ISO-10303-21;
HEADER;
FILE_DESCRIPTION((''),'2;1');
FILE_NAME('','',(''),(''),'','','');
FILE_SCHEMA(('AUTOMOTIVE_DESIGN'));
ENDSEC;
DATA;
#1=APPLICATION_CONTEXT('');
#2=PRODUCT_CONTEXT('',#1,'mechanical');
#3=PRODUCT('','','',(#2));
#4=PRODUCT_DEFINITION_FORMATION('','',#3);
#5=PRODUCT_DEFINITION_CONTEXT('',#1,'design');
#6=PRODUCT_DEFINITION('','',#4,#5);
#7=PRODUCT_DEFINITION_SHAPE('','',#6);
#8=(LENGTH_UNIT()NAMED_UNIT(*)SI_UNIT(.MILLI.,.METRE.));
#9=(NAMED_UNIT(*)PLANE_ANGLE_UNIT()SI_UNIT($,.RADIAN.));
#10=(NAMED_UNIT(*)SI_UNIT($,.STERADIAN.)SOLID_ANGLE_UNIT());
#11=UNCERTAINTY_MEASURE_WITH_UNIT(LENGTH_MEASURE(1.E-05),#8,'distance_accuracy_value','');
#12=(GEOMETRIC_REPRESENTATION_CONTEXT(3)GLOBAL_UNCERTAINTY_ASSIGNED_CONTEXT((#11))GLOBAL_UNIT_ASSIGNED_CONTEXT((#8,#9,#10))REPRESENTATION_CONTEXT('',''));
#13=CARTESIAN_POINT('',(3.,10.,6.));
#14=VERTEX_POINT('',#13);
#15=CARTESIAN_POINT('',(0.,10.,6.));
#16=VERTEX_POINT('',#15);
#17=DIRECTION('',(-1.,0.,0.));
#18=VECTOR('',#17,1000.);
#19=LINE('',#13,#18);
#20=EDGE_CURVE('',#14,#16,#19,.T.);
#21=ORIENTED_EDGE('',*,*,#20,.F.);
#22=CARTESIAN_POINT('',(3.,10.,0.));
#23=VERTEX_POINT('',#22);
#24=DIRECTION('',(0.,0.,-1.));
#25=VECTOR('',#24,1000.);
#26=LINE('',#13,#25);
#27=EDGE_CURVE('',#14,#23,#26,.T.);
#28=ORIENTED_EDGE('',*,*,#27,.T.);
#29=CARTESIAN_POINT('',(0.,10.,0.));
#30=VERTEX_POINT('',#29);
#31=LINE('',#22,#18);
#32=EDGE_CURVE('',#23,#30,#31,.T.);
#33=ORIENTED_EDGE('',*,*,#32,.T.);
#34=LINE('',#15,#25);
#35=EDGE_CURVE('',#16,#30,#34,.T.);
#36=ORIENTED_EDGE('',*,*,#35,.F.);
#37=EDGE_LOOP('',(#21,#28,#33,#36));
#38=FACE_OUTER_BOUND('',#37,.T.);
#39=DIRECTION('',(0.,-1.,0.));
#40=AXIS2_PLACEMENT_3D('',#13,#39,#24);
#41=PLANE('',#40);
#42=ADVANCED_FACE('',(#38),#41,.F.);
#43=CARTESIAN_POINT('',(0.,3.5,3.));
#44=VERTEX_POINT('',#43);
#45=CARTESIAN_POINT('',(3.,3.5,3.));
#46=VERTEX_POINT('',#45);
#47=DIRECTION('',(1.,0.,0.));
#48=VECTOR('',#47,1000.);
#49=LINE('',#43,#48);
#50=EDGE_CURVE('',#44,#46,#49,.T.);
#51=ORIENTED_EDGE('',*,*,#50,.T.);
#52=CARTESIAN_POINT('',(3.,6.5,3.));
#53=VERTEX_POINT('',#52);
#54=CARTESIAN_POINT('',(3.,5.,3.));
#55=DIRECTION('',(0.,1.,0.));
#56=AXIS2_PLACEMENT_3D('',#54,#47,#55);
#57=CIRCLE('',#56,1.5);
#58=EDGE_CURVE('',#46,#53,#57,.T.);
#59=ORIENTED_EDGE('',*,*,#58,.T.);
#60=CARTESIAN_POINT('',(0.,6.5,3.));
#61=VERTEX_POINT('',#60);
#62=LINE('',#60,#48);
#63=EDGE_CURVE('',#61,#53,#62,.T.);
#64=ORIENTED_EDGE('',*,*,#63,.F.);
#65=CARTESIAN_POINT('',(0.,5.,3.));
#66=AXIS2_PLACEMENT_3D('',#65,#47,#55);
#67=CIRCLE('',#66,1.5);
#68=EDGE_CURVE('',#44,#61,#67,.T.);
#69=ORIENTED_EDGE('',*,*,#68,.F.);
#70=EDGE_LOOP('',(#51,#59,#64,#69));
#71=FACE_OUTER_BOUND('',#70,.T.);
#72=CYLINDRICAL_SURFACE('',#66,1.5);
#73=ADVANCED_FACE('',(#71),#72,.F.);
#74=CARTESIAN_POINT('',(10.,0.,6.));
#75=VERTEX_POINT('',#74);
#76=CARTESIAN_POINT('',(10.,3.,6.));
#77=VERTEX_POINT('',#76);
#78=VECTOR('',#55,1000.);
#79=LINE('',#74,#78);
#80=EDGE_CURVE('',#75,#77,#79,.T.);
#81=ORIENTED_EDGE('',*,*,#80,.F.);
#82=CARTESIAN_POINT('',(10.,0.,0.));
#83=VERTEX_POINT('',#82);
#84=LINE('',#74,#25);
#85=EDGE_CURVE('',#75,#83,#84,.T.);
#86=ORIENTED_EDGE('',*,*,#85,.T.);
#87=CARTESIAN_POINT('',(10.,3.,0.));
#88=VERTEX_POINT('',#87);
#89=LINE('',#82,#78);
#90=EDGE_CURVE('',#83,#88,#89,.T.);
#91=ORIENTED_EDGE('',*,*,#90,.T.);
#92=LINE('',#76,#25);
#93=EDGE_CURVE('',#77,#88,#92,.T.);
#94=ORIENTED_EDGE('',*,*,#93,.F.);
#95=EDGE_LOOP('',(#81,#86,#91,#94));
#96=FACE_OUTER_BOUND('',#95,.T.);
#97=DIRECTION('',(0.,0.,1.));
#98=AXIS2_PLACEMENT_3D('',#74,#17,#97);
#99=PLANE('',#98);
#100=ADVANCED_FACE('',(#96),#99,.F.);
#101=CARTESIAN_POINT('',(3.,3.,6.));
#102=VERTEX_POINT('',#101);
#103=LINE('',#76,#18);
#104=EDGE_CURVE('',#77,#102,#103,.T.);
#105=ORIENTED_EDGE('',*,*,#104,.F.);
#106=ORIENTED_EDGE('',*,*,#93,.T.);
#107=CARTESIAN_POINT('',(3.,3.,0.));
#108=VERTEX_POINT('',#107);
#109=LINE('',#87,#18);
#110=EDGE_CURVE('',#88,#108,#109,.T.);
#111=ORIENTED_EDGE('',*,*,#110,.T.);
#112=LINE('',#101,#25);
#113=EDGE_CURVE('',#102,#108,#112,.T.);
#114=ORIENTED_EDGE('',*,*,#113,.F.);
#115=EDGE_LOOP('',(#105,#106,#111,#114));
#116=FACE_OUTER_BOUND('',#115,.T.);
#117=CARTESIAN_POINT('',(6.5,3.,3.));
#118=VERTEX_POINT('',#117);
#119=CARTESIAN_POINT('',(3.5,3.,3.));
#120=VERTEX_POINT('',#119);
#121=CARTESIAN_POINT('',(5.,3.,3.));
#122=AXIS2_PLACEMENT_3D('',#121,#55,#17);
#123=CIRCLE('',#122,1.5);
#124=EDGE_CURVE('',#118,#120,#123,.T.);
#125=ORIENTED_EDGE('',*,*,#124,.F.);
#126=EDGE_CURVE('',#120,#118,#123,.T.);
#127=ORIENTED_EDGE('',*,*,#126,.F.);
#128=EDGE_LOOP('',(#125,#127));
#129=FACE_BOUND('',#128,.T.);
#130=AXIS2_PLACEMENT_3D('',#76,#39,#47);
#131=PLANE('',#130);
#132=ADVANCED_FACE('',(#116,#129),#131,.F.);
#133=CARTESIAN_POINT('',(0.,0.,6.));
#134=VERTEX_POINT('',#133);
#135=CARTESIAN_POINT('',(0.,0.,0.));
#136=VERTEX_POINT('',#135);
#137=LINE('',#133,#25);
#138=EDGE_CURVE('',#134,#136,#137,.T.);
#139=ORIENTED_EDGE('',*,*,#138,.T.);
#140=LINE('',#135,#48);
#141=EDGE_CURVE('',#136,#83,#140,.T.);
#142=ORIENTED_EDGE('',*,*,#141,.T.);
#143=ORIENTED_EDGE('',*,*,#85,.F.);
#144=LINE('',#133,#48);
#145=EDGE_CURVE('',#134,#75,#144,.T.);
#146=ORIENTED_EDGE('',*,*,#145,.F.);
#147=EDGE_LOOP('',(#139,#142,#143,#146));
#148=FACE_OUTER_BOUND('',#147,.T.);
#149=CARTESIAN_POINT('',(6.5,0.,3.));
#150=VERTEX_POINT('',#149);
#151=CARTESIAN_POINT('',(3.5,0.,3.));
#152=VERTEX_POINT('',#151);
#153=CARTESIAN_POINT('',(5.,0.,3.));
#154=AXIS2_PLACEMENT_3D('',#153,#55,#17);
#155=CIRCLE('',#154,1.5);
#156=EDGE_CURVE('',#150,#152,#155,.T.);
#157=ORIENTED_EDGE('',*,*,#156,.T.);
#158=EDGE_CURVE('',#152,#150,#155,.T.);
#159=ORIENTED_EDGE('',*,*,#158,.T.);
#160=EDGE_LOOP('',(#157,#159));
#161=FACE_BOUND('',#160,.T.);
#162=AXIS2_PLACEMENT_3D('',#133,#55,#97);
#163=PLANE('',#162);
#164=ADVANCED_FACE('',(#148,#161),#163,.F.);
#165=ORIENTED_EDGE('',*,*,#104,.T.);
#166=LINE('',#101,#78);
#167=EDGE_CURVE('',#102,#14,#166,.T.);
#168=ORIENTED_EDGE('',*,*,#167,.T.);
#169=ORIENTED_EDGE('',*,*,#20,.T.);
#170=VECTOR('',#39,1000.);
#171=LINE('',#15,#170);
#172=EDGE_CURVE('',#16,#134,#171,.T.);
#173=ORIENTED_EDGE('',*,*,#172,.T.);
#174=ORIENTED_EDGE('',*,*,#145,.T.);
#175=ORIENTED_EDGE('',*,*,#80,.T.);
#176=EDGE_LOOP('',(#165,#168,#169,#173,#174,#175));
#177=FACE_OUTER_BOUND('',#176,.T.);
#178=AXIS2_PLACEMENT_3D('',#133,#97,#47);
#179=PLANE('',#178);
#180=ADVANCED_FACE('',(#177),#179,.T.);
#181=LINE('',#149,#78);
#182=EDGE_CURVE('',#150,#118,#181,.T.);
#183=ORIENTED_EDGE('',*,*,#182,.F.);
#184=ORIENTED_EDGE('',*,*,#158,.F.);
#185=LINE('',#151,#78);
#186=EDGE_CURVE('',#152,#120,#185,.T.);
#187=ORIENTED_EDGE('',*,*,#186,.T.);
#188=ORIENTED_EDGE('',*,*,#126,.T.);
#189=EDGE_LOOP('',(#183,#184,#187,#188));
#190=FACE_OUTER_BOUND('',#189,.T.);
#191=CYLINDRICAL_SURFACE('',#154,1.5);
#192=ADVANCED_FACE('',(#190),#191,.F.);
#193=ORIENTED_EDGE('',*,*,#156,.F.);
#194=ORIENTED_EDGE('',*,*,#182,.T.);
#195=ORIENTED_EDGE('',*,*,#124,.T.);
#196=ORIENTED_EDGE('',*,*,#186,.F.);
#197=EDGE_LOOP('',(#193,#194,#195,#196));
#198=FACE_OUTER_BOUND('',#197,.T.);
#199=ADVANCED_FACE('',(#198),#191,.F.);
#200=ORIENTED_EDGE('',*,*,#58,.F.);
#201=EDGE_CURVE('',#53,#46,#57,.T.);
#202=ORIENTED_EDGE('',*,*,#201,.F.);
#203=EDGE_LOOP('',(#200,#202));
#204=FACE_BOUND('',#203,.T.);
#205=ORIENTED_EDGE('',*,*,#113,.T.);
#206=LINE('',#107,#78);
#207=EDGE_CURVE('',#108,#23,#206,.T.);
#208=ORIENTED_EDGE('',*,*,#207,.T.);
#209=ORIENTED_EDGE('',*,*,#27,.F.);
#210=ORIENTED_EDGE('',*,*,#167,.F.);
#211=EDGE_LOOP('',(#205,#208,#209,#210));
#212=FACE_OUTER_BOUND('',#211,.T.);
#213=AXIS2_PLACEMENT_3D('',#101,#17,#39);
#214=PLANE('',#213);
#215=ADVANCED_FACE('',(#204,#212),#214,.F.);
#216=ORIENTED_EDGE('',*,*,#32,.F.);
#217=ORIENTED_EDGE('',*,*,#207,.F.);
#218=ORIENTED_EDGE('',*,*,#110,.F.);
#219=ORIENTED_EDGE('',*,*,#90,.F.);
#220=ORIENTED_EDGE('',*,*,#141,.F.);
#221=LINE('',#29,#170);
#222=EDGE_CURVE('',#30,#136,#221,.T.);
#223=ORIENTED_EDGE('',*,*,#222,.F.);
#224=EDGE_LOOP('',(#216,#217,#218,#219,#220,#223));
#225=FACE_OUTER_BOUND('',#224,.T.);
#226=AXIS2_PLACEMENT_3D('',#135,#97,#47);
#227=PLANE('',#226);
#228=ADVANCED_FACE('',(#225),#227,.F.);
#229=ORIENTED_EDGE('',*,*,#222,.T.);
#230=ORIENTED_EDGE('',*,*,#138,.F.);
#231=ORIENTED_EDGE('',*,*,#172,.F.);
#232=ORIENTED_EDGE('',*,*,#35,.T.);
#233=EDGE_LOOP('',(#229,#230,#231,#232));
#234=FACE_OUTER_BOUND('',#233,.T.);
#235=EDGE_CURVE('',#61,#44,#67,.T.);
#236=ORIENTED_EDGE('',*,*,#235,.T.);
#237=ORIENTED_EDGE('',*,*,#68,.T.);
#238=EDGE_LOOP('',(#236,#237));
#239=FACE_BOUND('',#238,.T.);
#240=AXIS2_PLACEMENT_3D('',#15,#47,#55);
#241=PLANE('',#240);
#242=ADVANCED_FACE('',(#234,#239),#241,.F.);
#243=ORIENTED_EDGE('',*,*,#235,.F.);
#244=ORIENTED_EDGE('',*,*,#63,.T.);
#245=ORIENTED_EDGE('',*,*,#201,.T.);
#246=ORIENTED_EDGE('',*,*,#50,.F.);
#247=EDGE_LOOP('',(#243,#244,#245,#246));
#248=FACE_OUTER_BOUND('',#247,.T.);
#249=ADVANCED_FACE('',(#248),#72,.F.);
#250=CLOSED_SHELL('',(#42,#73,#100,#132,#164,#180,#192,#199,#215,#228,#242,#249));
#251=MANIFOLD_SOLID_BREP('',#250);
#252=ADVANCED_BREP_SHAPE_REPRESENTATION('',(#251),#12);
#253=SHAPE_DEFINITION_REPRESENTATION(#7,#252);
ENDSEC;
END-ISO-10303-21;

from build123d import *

# Parameters (mm, degrees)
EXTRUDE_4_DEPTH     = 6
SKETCH_7_R          = 1.5
CUT_EXTRUDE_3_DEPTH = 14.601470509
SKETCH_8_R          = 1.5
CUT_EXTRUDE_4_DEPTH = 14.601470509


with BuildPart() as part:
    # 草图6 → 凸台-拉伸4 (new body)
    with BuildSketch(Plane.XY):
        Polygon((0, 0), (10, 0), (10, 3), (3, 3), (3, 10), (0, 10), align=None)
    extrude(amount=EXTRUDE_4_DEPTH)

    # 草图7 → 切除-拉伸3 (cut, through all)
    with BuildSketch(Plane(origin=(3, 0, 0), x_dir=(0, 0, -1), z_dir=(1, 0, 0))):
        with Locations(Location((-3, 5, 0), (0, 0, 90))):
            Circle(SKETCH_7_R)
    extrude(amount=-CUT_EXTRUDE_3_DEPTH, mode=Mode.SUBTRACT)

    # 草图8 → 切除-拉伸4 (cut, through all)
    with BuildSketch(Plane(origin=(0, 3, 0), x_dir=(1, 0, 0), z_dir=(0, 1, 0))):
        with Locations(Location((5, -3, 0), (0, 0, 180))):
            Circle(SKETCH_8_R)
    extrude(amount=-CUT_EXTRUDE_4_DEPTH, mode=Mode.SUBTRACT)


solid = part.part
